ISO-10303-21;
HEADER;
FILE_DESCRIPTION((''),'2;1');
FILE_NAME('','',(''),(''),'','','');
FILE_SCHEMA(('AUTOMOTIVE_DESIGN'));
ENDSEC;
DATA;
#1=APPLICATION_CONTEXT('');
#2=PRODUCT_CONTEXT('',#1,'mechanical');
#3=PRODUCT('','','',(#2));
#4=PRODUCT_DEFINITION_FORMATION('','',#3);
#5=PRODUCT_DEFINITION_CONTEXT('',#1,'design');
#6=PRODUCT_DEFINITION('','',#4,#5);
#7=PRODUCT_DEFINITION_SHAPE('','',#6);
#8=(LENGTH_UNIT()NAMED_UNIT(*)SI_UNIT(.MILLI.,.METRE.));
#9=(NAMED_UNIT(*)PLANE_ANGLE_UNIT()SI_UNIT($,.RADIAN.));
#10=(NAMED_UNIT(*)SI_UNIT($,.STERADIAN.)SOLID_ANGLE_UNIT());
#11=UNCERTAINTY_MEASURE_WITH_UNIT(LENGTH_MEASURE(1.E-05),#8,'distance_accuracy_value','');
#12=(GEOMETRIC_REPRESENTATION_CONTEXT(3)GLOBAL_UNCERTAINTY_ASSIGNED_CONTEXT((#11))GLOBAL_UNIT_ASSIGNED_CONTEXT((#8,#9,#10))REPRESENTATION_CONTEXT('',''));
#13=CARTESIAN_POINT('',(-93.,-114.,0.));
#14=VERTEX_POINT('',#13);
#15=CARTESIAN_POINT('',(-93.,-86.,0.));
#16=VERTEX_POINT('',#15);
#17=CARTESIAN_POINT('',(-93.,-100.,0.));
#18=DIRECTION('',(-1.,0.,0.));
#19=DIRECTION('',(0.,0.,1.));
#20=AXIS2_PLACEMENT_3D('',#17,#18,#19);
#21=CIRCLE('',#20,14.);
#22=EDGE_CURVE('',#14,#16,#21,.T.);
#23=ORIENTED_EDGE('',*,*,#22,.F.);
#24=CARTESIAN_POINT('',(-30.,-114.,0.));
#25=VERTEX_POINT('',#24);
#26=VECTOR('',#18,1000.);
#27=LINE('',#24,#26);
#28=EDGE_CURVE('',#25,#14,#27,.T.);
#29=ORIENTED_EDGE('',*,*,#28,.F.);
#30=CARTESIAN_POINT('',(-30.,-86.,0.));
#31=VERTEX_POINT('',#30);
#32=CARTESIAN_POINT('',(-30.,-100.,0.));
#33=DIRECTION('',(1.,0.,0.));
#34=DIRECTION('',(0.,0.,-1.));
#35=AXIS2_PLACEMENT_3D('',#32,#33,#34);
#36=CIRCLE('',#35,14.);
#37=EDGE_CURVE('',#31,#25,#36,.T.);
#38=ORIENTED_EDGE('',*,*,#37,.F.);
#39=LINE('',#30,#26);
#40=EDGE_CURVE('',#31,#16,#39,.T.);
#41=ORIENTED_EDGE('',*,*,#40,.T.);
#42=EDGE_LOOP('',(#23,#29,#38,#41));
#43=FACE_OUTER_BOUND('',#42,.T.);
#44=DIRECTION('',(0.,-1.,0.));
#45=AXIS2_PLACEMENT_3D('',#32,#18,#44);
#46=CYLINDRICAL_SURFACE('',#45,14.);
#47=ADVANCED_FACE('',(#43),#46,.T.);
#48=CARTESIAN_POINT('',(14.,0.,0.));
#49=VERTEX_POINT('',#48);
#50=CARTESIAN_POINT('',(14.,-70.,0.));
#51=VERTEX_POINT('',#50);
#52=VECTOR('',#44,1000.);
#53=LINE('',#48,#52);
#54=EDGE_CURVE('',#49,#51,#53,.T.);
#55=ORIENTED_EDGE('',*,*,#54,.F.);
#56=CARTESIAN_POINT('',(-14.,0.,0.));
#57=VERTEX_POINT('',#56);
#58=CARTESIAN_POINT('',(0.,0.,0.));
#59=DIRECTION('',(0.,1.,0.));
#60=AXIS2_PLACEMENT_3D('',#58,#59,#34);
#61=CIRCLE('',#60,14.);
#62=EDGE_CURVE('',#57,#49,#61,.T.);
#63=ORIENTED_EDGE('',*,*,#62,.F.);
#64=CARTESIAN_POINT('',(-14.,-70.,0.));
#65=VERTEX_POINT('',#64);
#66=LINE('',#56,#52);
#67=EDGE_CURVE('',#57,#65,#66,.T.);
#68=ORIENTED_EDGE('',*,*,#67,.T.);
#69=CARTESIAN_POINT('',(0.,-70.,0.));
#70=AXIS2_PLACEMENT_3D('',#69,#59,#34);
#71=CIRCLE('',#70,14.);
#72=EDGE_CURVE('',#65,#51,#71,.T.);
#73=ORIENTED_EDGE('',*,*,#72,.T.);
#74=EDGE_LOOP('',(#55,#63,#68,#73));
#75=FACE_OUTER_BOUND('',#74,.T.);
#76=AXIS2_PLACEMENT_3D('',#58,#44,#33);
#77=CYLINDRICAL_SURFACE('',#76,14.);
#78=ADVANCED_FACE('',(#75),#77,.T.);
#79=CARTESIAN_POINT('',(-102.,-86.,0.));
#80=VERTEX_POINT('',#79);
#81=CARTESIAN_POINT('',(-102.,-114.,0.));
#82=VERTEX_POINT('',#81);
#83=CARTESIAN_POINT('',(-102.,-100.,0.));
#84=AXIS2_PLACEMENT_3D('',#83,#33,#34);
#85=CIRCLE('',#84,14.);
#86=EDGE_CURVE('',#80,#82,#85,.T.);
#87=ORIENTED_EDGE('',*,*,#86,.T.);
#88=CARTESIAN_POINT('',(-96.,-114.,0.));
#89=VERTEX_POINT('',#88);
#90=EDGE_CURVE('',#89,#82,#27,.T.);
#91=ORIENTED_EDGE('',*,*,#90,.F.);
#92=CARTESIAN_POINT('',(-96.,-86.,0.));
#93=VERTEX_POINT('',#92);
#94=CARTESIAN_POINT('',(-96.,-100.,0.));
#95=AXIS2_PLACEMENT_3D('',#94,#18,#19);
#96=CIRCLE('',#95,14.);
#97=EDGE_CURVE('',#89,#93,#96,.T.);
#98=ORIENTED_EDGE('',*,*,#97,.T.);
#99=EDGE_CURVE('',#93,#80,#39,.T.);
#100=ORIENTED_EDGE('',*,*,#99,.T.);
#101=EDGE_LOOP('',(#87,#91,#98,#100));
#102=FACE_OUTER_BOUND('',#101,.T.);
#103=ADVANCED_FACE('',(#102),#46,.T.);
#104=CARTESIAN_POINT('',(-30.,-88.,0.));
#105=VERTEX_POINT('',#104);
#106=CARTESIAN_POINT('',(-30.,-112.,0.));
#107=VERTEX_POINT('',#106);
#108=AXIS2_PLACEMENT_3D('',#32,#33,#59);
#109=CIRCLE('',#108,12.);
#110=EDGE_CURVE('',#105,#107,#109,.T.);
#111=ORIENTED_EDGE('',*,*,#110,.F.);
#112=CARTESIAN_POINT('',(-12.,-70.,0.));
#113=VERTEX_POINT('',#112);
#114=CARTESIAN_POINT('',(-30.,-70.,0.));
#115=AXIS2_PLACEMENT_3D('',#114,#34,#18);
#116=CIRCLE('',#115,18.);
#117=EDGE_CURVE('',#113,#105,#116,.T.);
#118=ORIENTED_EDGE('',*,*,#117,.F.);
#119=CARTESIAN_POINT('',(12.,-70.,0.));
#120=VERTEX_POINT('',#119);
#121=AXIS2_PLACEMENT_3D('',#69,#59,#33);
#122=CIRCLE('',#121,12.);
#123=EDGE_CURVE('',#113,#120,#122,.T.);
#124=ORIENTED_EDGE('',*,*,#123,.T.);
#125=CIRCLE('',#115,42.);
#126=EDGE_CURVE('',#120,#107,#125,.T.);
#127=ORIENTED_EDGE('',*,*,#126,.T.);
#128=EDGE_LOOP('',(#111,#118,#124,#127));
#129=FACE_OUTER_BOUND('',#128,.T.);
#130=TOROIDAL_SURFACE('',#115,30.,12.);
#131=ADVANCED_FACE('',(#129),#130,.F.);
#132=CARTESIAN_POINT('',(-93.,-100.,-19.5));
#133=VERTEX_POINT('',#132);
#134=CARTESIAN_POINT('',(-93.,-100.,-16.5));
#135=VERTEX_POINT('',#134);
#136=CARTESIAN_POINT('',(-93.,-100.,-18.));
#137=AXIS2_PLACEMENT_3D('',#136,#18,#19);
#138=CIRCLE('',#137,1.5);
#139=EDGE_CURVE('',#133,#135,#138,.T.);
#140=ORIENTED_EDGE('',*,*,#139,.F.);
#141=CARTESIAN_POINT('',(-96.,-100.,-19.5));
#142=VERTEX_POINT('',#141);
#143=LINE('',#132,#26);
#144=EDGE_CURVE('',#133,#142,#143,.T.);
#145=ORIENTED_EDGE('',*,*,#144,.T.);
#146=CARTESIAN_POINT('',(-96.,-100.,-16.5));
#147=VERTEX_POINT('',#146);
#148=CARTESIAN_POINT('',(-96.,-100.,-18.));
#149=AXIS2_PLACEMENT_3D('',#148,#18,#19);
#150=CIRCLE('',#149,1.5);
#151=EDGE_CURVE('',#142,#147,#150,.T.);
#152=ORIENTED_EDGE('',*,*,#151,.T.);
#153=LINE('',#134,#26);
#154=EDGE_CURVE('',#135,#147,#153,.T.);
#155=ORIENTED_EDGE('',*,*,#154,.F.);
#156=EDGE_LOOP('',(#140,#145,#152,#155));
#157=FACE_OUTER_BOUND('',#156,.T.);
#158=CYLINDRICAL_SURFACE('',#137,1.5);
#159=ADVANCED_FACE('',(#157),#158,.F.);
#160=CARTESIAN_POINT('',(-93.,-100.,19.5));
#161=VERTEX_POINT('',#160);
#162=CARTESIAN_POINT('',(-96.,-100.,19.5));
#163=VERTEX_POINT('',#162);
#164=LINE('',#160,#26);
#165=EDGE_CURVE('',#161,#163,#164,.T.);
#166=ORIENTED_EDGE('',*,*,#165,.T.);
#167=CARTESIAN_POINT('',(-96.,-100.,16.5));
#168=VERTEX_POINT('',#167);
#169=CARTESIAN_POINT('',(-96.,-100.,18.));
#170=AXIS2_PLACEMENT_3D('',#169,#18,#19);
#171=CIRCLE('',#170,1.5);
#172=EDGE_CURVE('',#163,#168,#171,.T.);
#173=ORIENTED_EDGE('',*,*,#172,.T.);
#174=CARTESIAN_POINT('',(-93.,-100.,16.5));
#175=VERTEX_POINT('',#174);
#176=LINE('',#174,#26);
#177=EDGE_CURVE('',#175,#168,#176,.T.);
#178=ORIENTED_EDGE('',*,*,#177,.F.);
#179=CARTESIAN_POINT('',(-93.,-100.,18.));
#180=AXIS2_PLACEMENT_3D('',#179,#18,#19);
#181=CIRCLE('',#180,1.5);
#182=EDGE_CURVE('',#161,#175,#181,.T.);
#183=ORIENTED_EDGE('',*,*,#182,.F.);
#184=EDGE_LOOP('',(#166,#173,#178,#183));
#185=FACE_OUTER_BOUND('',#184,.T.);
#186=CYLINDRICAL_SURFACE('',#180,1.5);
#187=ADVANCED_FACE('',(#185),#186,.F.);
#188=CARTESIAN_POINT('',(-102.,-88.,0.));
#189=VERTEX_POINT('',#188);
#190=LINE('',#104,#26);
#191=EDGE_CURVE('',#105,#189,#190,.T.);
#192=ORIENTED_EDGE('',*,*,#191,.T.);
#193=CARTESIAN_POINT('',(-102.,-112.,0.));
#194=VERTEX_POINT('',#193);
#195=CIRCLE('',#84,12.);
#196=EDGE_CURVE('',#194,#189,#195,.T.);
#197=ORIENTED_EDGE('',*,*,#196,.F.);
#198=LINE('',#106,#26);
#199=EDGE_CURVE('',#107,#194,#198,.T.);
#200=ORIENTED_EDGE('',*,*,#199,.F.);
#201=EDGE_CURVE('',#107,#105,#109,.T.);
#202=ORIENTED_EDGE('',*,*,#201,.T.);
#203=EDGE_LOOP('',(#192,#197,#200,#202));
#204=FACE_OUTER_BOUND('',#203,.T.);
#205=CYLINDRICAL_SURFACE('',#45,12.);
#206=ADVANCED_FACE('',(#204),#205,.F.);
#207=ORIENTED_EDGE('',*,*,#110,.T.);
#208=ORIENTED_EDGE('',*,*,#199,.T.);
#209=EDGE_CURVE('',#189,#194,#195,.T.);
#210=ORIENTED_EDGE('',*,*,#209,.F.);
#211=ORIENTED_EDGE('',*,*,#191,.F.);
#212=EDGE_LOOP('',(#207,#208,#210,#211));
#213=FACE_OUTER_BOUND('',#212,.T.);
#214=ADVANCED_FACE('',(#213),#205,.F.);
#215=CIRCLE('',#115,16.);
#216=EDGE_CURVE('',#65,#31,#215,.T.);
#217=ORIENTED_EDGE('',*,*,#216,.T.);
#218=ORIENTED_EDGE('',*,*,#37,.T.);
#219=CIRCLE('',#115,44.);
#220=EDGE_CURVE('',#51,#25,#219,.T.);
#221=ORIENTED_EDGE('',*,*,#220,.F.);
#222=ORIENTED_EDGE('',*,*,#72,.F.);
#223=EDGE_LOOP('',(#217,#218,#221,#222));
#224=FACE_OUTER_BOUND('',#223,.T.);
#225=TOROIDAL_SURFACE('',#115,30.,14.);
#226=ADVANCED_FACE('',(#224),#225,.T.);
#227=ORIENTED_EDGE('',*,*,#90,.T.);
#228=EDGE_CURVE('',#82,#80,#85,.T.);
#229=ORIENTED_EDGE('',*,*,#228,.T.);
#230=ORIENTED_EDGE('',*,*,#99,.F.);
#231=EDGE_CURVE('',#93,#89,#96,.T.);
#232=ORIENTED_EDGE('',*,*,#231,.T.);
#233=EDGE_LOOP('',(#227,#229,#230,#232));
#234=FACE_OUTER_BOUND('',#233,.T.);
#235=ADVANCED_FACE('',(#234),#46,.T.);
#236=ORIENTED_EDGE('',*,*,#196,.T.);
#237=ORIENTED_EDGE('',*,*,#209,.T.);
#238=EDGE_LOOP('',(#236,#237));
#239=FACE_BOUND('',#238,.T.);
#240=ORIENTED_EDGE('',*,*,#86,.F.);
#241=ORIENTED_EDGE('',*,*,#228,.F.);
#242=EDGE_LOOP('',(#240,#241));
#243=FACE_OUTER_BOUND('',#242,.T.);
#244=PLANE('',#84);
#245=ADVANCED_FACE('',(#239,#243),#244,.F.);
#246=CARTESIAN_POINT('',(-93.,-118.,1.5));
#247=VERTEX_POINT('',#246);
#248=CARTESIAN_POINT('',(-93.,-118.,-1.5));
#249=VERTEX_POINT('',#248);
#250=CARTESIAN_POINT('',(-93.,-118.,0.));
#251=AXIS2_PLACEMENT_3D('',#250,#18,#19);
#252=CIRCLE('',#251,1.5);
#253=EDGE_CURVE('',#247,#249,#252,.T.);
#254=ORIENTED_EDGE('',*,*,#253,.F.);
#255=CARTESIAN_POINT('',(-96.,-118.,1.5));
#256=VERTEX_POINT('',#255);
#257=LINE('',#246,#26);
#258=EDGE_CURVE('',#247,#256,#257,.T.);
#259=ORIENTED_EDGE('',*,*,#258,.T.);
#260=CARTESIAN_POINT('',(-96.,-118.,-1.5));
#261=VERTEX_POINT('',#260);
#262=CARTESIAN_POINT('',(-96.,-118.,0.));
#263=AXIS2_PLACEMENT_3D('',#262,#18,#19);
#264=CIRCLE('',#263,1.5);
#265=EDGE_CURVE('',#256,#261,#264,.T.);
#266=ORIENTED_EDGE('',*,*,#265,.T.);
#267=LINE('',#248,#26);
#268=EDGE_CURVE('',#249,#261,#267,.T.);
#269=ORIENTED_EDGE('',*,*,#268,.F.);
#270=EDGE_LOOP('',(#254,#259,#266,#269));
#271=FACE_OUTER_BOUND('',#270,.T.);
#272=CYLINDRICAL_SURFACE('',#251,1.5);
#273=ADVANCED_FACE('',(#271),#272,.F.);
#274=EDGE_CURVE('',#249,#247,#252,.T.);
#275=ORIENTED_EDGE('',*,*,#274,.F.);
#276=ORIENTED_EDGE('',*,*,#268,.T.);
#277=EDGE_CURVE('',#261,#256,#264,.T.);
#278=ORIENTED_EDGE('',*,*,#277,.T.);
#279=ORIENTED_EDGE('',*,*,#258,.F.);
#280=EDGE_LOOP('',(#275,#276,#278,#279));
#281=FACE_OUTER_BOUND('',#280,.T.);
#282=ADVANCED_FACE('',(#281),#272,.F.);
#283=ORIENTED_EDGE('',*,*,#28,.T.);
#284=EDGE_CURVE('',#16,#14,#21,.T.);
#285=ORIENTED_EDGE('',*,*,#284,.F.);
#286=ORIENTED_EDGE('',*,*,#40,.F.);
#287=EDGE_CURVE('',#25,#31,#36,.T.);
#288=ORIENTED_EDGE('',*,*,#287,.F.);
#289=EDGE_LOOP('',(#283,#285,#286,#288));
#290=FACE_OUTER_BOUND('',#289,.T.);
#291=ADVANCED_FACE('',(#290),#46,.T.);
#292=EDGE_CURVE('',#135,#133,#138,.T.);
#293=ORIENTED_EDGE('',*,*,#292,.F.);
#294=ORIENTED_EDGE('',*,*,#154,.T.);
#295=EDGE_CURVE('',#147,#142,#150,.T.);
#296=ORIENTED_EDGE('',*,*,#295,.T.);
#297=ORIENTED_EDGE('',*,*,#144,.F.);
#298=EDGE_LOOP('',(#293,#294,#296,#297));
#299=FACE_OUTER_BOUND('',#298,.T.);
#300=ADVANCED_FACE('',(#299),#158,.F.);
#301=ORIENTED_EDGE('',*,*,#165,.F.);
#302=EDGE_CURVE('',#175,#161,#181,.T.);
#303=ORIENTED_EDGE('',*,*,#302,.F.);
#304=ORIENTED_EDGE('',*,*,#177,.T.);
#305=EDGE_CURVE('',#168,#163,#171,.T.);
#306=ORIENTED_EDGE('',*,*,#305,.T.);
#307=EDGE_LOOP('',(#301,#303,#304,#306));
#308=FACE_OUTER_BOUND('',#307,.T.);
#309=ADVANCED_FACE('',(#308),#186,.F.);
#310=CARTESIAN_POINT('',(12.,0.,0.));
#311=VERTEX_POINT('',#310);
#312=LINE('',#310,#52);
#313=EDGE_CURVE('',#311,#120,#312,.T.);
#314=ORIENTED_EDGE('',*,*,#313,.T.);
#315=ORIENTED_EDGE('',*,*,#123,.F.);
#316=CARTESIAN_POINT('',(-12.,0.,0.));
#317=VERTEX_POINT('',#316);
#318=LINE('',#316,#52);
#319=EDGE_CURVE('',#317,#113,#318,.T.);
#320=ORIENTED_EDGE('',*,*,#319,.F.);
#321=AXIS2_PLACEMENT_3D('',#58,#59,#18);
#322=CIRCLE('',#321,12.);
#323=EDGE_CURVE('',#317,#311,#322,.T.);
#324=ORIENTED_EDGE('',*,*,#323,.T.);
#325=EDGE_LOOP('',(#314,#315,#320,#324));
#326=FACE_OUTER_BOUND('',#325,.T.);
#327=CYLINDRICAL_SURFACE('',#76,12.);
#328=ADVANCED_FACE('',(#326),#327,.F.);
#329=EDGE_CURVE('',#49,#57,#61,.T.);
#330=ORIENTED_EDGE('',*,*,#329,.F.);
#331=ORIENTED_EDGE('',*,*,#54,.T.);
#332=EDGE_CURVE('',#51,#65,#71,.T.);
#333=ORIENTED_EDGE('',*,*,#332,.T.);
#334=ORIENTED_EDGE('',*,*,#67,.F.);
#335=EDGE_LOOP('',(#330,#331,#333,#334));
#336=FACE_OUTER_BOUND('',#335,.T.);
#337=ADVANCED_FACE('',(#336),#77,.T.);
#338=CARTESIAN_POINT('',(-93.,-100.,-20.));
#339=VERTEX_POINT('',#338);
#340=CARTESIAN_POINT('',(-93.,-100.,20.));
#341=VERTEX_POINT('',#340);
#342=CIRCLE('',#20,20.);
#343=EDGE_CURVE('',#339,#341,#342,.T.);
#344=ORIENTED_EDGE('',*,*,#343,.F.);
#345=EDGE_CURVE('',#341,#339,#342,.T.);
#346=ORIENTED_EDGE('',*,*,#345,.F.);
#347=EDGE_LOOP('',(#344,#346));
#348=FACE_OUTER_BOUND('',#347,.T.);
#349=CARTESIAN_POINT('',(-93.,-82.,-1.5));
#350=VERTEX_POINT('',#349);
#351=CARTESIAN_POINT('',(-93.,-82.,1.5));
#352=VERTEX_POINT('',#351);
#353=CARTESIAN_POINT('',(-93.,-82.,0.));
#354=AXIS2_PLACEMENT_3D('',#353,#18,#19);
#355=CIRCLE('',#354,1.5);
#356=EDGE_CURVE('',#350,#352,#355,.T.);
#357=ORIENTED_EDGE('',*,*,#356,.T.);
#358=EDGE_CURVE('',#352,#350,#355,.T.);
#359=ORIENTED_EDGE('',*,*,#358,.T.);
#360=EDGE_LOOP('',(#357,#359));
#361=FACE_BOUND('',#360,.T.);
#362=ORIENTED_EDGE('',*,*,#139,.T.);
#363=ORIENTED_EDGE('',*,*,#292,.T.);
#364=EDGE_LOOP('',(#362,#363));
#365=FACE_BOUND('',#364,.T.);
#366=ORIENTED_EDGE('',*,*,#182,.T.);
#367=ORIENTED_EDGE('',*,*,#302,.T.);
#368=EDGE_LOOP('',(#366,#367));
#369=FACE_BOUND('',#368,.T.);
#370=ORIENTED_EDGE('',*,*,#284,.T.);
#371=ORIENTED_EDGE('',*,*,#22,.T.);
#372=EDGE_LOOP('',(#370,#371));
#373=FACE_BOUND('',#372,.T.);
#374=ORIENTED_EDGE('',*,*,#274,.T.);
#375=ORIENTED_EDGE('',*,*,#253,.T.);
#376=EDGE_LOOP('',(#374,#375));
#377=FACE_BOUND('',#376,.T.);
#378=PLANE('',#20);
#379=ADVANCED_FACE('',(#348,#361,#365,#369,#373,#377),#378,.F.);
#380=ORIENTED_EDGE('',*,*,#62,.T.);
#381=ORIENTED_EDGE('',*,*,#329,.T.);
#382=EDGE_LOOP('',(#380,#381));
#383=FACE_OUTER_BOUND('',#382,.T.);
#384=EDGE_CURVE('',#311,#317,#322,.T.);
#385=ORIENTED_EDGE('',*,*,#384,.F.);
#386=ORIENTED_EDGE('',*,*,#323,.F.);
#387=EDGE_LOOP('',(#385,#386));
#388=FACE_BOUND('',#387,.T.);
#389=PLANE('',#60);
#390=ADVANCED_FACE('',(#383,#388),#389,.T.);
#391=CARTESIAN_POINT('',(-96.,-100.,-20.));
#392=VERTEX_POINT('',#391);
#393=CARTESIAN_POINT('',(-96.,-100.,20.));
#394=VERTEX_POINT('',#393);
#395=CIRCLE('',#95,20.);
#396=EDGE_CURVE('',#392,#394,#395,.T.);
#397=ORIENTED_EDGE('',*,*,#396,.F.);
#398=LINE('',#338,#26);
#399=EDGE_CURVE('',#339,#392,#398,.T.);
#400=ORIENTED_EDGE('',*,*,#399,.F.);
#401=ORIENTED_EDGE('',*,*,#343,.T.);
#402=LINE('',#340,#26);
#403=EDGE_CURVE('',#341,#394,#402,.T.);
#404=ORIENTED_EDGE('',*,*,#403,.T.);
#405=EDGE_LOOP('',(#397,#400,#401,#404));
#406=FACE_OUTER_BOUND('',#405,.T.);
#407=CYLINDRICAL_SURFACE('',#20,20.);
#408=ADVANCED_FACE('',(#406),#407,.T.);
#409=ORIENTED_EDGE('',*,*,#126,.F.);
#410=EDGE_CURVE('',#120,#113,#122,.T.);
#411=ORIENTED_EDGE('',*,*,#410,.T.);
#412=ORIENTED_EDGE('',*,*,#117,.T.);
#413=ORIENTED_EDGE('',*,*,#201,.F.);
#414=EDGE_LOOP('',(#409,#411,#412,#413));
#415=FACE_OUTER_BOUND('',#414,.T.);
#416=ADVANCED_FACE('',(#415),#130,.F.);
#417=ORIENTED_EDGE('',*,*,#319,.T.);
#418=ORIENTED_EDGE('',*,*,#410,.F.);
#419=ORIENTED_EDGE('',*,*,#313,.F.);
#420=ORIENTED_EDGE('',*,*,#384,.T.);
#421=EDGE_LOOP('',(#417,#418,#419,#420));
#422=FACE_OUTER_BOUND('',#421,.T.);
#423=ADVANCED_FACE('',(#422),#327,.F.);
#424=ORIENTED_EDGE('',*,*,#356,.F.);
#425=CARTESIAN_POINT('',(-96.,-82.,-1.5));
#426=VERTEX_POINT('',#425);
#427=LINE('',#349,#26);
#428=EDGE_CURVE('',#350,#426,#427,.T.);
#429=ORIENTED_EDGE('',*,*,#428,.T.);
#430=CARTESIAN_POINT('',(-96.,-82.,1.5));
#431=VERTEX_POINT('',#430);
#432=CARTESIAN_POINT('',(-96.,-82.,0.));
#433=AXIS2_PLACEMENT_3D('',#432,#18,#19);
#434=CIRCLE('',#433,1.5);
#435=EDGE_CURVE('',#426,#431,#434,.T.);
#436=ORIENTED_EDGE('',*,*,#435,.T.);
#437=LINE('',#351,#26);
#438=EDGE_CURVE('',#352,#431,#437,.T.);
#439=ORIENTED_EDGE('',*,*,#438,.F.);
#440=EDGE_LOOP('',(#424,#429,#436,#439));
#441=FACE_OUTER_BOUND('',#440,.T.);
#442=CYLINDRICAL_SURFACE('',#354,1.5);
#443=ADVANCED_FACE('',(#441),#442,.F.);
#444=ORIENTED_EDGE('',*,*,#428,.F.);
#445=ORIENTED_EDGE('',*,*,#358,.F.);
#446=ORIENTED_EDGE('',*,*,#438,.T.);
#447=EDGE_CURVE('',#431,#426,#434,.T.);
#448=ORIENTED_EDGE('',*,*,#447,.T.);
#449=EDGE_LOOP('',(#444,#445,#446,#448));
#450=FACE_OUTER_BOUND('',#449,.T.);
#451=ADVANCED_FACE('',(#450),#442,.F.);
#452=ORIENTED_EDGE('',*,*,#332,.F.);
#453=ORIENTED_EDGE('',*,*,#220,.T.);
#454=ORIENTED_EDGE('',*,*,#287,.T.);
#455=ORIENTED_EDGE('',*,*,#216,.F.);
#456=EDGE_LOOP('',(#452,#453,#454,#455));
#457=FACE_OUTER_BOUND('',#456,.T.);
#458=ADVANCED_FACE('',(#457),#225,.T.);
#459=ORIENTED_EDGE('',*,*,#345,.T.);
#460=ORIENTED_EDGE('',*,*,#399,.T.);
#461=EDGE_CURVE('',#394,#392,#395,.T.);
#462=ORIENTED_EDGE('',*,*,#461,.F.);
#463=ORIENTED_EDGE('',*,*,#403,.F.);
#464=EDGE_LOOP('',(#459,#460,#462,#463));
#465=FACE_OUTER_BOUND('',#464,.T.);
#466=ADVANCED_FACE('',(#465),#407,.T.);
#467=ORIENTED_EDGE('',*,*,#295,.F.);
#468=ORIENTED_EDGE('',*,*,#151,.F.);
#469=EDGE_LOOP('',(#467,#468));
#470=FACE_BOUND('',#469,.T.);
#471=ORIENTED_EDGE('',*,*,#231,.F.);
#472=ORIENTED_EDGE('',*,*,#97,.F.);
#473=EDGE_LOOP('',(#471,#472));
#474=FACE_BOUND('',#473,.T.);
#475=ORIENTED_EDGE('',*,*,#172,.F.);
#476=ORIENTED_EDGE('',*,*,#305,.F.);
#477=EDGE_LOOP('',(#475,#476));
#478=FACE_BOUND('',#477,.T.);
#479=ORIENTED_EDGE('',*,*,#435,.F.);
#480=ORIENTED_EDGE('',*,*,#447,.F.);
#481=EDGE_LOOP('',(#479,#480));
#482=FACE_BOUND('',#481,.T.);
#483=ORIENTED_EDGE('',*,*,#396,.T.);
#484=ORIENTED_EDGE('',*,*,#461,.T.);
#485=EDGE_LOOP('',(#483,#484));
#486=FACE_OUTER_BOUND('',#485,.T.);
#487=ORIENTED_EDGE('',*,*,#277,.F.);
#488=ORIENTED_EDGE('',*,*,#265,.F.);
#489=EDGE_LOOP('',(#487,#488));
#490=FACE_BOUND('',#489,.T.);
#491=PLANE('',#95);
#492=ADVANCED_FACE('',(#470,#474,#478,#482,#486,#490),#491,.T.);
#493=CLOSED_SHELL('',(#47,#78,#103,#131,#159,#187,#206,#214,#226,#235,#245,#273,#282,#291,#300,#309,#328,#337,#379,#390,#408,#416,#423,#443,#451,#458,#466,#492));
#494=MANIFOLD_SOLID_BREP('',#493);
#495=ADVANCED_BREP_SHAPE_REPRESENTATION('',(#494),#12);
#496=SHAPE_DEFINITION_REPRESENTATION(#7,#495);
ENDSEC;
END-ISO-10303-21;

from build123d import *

# Parameters (mm, degrees)
SWEEP1_PROFILE_R    = 14
SHELL1_T            = -2
BOSS_EXTRUDE1_START = -6
SKETCH6_R           = 20
SKETCH6_R_2         = 12
SKETCH6_R_3         = 1.5
BOSS_EXTRUDE1_DEPTH = 3


with BuildPart() as part:
    # Sweep1: sweep along a path in Sketch1
    with BuildLine(Plane.XY) as sweep1_path:
        Line((0, 0), (0, -70))
        ThreePointArc((0, -70), (-8.786796564, -91.213203436), (-30, -100))
        Line((-30, -100), (-102, -100))
    # Sweep1 profile (on start of the path) → Sweep1 (sweep)
    with BuildSketch(Plane(origin=(0, 0, 0), x_dir=(-1, 0, 0), z_dir=(0, -1, 0))):
        Circle(SWEEP1_PROFILE_R)
    sweep(path=sweep1_path.line)

    # Shell1
    shell1_openings = [part.faces().sort_by_distance(p)[0] for p in [
        (-102, -100, 0),
        (0, 0, 0),
    ]]
    offset(amount=SHELL1_T, openings=shell1_openings, kind=Kind.INTERSECTION)

    # Sketch6 → Boss-Extrude1 (add)
    with BuildSketch(Plane.ZY.offset(102).offset(BOSS_EXTRUDE1_START)):
        with Locations((0, -100)):
            Circle(SKETCH6_R)
        with Locations(Location((0, -100, 0), (0, 0, 270))):
            Circle(SKETCH6_R_2, mode=Mode.SUBTRACT)
        with Locations((0, -82)):
            Circle(SKETCH6_R_3, mode=Mode.SUBTRACT)
        with Locations((18, -100)):
            Circle(SKETCH6_R_3, mode=Mode.SUBTRACT)
        with Locations((0, -118)):
            Circle(SKETCH6_R_3, mode=Mode.SUBTRACT)
        with Locations((-18, -100)):
            Circle(SKETCH6_R_3, mode=Mode.SUBTRACT)
    extrude(amount=-BOSS_EXTRUDE1_DEPTH)


solid = part.part
